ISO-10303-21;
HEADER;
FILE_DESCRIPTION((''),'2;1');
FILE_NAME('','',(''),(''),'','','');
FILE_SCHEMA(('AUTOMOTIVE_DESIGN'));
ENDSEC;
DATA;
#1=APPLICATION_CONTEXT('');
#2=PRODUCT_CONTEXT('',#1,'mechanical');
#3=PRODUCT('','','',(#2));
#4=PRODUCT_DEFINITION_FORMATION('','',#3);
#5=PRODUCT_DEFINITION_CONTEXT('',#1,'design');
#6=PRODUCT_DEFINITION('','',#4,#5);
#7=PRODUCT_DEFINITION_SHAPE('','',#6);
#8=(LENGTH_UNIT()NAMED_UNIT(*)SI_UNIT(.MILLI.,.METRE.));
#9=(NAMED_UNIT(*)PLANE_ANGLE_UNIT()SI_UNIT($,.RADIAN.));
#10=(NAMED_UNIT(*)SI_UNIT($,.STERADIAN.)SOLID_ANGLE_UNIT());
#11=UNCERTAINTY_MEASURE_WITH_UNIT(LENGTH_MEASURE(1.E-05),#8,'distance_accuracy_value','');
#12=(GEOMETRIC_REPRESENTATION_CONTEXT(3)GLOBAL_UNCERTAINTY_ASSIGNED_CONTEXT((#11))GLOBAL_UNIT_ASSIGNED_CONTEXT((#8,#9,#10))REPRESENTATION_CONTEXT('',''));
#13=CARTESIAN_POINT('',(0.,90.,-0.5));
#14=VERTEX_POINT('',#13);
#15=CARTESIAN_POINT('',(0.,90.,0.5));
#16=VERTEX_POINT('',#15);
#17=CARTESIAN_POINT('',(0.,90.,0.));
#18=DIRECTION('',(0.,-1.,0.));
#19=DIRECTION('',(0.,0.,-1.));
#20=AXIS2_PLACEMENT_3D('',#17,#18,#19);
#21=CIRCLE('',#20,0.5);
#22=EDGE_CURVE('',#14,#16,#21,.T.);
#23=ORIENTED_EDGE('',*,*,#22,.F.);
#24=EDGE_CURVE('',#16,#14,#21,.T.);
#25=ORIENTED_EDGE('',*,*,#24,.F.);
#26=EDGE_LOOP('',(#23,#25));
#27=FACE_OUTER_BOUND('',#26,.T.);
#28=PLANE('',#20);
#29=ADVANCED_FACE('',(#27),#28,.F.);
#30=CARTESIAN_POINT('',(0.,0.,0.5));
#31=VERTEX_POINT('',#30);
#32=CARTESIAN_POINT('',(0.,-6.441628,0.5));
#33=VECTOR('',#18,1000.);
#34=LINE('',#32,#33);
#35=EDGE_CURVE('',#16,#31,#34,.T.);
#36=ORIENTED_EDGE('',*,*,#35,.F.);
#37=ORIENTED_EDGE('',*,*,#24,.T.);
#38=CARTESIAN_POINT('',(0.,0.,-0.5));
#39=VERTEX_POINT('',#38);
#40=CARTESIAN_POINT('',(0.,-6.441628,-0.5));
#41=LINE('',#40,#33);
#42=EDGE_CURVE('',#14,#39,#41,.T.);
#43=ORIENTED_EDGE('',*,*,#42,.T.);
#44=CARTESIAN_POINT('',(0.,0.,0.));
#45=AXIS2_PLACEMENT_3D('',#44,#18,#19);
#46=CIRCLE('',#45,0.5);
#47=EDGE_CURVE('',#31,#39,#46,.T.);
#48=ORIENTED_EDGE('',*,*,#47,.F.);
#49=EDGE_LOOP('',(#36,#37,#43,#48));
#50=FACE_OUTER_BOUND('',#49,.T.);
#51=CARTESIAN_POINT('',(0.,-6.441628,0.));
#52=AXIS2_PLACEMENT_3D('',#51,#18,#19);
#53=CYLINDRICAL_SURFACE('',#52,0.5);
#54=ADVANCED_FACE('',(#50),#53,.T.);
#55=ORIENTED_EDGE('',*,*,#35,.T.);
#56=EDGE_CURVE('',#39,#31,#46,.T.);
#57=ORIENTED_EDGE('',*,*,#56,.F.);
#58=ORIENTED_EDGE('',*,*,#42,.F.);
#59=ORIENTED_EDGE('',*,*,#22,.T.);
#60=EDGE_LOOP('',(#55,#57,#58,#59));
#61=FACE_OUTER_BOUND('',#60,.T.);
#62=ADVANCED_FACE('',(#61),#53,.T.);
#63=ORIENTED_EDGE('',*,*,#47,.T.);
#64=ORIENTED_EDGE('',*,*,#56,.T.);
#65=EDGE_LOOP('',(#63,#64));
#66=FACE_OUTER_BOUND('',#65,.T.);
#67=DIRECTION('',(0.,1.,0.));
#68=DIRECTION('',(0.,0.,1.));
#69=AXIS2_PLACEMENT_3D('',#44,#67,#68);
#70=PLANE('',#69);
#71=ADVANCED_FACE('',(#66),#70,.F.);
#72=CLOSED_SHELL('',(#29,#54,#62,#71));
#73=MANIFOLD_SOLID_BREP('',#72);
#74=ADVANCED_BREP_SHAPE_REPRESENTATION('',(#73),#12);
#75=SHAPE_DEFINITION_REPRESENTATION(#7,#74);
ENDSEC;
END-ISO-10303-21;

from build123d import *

# Parameters (mm, degrees)
SKETCH1_W = 0.5
SKETCH1_H = 90


with BuildPart() as part:
    # Sketch1 → Revolve1 (revolve)
    with BuildSketch(Plane.XY, mode=Mode.PRIVATE) as revolve1_sk:
        with Locations((-0.25, 45)):
            Rectangle(SKETCH1_W, SKETCH1_H)
    revolve(revolve1_sk.sketch.rotate(Axis((0, -6.441627678, 0), (0, 1, 0)), 270), axis=Axis((0, -6.441627678, 0), (0, 1, 0)))


solid = part.part
